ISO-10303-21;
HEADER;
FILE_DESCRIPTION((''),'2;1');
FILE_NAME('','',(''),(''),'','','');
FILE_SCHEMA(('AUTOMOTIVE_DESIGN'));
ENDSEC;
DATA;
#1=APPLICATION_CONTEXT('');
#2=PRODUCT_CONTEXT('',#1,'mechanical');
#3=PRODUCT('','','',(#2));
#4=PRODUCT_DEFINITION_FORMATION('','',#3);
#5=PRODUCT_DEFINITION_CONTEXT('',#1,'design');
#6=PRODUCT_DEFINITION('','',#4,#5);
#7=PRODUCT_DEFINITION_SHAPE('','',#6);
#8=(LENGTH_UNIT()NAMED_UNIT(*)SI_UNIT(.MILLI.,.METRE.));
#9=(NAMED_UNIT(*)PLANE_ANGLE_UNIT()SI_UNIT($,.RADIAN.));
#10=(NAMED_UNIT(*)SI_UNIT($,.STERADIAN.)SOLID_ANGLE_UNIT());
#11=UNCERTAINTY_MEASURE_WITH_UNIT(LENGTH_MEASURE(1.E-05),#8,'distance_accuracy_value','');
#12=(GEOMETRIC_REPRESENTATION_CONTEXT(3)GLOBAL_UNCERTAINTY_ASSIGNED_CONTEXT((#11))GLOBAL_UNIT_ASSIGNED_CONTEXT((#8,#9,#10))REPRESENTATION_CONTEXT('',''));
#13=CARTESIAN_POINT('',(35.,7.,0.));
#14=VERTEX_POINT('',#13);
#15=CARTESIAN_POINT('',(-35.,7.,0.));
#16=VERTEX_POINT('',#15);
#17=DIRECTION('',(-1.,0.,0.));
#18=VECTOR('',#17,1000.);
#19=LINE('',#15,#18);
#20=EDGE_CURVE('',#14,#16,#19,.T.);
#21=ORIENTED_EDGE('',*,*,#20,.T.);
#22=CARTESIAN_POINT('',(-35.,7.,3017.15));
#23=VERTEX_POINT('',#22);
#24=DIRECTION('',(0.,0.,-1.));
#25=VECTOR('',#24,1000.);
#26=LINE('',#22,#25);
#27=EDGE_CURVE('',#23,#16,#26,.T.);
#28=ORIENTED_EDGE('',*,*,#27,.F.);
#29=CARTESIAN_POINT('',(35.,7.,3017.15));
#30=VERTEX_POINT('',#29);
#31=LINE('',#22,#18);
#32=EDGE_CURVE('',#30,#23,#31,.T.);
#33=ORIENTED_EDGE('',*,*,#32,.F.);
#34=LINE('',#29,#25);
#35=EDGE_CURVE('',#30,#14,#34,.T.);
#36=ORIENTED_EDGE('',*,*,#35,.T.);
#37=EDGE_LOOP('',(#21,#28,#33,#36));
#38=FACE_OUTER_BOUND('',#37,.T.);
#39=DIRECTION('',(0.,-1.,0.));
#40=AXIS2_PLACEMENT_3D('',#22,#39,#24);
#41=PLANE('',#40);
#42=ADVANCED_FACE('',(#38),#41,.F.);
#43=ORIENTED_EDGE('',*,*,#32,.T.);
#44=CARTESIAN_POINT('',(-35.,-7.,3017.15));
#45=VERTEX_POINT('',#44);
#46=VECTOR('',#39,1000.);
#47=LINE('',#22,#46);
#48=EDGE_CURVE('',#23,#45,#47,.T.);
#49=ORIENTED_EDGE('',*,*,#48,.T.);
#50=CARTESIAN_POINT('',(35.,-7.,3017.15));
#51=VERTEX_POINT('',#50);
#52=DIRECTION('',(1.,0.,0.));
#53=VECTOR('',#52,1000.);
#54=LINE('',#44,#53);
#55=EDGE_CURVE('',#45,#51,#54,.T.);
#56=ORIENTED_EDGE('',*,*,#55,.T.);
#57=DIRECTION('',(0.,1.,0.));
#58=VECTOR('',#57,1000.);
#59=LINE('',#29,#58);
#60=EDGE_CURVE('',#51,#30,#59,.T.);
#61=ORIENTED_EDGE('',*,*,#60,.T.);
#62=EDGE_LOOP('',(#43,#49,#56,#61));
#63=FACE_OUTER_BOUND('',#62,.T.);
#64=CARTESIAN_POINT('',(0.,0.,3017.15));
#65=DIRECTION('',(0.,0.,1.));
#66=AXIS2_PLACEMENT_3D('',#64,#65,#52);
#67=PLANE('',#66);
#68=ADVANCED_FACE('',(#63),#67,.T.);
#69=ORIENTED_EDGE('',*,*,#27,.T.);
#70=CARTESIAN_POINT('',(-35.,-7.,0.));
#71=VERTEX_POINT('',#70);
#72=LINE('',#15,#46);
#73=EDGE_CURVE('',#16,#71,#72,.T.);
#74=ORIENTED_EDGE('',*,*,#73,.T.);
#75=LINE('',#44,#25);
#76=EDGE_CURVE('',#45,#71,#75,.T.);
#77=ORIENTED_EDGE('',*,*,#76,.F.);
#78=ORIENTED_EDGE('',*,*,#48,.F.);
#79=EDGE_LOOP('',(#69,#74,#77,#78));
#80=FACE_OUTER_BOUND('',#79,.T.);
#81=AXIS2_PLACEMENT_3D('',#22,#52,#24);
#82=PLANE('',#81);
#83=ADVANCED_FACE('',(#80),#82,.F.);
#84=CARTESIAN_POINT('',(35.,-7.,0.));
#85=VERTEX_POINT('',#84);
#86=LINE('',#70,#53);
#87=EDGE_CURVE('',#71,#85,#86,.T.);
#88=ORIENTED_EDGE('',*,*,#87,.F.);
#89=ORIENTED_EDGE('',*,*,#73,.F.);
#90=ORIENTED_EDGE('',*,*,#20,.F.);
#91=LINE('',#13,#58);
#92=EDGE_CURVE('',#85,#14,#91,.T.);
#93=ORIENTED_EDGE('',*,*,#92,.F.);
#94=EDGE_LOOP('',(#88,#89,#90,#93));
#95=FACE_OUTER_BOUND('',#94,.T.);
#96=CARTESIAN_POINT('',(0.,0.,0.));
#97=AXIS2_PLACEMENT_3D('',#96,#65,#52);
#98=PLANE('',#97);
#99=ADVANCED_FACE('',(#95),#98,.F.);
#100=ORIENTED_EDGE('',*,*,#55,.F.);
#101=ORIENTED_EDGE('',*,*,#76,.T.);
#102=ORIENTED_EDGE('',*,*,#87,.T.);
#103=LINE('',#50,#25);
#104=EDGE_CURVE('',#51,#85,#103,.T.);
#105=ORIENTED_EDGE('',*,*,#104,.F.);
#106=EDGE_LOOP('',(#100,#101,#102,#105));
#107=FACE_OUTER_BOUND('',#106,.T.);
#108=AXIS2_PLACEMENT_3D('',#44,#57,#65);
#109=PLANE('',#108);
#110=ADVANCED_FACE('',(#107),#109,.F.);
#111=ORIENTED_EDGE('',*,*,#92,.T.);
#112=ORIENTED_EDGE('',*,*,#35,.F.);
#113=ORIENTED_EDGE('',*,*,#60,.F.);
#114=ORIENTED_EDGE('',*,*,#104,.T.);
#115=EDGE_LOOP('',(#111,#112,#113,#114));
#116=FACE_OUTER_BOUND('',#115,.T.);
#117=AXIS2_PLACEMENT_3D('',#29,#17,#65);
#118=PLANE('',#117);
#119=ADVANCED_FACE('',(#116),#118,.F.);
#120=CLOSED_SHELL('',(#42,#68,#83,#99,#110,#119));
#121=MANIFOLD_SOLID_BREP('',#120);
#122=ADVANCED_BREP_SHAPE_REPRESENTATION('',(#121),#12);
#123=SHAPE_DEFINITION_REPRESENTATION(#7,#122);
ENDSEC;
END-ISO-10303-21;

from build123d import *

# Parameters (mm, degrees)
SKETCH1_W           = 70
SKETCH1_H           = 14
BOSS_EXTRUDE1_DEPTH = 3017.15


with BuildPart() as part:
    # Sketch1 → Boss-Extrude1 (new body)
    with BuildSketch(Plane.XY):
        Rectangle(SKETCH1_W, SKETCH1_H)
    extrude(amount=BOSS_EXTRUDE1_DEPTH)


solid = part.part
